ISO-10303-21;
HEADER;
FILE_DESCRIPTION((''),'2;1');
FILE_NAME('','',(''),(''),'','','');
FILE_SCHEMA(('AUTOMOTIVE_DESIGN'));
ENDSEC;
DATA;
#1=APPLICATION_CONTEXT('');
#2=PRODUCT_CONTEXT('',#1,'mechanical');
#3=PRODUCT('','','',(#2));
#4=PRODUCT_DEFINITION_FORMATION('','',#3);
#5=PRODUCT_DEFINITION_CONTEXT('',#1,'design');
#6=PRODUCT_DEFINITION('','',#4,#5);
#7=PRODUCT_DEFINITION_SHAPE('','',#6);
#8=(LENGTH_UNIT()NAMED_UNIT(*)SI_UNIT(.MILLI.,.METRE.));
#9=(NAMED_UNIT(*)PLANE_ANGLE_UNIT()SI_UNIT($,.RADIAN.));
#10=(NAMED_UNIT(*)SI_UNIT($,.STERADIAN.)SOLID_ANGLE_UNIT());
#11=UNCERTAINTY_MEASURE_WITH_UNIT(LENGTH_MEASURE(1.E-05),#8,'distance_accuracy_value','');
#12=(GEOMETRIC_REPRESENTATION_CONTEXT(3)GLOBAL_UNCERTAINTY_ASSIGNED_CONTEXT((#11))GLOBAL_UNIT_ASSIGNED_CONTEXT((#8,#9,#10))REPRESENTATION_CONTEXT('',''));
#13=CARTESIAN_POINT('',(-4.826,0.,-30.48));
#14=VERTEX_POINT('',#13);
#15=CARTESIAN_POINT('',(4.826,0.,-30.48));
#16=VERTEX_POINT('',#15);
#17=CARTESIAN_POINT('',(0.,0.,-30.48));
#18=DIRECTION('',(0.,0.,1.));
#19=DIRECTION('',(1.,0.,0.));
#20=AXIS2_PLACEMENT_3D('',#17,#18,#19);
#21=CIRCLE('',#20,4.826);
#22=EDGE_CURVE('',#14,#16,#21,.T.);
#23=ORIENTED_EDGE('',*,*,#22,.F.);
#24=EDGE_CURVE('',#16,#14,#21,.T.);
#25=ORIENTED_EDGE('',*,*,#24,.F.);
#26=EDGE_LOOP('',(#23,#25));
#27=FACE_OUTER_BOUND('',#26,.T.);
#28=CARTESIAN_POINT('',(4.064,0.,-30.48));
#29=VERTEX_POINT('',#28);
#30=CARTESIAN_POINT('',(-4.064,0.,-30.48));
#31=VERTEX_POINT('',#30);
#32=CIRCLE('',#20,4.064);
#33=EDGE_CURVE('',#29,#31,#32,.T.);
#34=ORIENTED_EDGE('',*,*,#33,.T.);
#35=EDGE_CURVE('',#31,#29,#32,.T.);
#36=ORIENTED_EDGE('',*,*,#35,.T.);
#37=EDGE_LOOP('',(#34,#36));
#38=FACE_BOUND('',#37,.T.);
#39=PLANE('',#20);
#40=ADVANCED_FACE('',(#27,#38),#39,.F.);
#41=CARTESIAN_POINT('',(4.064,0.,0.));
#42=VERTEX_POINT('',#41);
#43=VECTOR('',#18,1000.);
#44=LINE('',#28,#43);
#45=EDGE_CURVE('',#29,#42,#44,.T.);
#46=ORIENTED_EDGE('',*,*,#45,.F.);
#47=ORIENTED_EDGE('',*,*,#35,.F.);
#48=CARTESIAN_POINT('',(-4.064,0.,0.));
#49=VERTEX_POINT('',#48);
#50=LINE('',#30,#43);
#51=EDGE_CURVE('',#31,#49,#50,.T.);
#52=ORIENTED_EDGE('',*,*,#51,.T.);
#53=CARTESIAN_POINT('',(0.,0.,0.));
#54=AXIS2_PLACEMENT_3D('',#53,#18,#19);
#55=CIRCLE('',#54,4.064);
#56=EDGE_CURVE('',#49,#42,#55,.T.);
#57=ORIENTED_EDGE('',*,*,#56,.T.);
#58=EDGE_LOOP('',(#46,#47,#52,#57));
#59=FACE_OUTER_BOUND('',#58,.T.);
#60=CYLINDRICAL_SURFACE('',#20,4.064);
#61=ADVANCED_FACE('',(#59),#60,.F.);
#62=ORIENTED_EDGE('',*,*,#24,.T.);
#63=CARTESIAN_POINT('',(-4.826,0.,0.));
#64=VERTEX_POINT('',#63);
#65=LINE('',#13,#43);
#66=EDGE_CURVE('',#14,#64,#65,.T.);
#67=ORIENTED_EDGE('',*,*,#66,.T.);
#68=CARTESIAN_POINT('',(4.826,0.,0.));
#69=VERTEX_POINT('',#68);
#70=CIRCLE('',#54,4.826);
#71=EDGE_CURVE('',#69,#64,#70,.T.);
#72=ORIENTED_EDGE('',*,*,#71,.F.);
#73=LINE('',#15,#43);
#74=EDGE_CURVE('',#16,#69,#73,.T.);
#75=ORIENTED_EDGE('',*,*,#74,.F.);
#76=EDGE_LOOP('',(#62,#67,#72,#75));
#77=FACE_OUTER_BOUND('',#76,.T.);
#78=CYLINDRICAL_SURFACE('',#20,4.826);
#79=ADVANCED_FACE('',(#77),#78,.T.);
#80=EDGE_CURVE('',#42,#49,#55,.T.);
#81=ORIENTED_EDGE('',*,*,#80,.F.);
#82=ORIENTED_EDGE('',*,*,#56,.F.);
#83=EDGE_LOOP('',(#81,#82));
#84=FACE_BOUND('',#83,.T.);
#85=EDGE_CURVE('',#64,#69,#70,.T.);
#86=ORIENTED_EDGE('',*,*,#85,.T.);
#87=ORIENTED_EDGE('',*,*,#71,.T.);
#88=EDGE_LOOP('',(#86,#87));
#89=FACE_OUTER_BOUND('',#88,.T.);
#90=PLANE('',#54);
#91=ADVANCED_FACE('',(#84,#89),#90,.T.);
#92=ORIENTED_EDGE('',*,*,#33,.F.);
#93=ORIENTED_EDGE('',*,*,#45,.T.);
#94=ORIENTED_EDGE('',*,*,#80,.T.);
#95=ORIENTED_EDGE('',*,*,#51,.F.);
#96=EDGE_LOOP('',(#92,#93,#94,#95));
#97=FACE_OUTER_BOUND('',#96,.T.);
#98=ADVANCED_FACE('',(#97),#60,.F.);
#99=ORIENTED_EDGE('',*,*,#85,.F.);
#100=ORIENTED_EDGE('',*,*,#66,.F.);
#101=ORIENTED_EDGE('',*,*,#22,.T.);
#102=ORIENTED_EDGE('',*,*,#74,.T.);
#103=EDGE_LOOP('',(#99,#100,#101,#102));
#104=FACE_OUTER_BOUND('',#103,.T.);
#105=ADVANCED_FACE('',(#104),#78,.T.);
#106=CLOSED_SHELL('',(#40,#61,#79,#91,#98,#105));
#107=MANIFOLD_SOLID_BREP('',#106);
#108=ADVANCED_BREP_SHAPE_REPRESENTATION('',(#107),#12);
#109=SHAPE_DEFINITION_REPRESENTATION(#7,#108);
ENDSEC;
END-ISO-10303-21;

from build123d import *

# Parameters (mm, degrees)
SKETCH1_R           = 2.413
SKETCH1_R_2         = 2.032
BOSS_EXTRUDE1_DEPTH = 15.24
SCALE1_SCALE        = 2


with BuildPart() as part:
    # Sketch1 → Boss-Extrude1 (new body)
    with BuildSketch(Plane.XY):
        Circle(SKETCH1_R)
        Circle(SKETCH1_R_2, mode=Mode.SUBTRACT)
    extrude(amount=-BOSS_EXTRUDE1_DEPTH)


with BuildPart() as part_1:
    # Scale1: scaled about (0, 0, 0)
    add(part.part.scale(SCALE1_SCALE))


solid = part_1.part
